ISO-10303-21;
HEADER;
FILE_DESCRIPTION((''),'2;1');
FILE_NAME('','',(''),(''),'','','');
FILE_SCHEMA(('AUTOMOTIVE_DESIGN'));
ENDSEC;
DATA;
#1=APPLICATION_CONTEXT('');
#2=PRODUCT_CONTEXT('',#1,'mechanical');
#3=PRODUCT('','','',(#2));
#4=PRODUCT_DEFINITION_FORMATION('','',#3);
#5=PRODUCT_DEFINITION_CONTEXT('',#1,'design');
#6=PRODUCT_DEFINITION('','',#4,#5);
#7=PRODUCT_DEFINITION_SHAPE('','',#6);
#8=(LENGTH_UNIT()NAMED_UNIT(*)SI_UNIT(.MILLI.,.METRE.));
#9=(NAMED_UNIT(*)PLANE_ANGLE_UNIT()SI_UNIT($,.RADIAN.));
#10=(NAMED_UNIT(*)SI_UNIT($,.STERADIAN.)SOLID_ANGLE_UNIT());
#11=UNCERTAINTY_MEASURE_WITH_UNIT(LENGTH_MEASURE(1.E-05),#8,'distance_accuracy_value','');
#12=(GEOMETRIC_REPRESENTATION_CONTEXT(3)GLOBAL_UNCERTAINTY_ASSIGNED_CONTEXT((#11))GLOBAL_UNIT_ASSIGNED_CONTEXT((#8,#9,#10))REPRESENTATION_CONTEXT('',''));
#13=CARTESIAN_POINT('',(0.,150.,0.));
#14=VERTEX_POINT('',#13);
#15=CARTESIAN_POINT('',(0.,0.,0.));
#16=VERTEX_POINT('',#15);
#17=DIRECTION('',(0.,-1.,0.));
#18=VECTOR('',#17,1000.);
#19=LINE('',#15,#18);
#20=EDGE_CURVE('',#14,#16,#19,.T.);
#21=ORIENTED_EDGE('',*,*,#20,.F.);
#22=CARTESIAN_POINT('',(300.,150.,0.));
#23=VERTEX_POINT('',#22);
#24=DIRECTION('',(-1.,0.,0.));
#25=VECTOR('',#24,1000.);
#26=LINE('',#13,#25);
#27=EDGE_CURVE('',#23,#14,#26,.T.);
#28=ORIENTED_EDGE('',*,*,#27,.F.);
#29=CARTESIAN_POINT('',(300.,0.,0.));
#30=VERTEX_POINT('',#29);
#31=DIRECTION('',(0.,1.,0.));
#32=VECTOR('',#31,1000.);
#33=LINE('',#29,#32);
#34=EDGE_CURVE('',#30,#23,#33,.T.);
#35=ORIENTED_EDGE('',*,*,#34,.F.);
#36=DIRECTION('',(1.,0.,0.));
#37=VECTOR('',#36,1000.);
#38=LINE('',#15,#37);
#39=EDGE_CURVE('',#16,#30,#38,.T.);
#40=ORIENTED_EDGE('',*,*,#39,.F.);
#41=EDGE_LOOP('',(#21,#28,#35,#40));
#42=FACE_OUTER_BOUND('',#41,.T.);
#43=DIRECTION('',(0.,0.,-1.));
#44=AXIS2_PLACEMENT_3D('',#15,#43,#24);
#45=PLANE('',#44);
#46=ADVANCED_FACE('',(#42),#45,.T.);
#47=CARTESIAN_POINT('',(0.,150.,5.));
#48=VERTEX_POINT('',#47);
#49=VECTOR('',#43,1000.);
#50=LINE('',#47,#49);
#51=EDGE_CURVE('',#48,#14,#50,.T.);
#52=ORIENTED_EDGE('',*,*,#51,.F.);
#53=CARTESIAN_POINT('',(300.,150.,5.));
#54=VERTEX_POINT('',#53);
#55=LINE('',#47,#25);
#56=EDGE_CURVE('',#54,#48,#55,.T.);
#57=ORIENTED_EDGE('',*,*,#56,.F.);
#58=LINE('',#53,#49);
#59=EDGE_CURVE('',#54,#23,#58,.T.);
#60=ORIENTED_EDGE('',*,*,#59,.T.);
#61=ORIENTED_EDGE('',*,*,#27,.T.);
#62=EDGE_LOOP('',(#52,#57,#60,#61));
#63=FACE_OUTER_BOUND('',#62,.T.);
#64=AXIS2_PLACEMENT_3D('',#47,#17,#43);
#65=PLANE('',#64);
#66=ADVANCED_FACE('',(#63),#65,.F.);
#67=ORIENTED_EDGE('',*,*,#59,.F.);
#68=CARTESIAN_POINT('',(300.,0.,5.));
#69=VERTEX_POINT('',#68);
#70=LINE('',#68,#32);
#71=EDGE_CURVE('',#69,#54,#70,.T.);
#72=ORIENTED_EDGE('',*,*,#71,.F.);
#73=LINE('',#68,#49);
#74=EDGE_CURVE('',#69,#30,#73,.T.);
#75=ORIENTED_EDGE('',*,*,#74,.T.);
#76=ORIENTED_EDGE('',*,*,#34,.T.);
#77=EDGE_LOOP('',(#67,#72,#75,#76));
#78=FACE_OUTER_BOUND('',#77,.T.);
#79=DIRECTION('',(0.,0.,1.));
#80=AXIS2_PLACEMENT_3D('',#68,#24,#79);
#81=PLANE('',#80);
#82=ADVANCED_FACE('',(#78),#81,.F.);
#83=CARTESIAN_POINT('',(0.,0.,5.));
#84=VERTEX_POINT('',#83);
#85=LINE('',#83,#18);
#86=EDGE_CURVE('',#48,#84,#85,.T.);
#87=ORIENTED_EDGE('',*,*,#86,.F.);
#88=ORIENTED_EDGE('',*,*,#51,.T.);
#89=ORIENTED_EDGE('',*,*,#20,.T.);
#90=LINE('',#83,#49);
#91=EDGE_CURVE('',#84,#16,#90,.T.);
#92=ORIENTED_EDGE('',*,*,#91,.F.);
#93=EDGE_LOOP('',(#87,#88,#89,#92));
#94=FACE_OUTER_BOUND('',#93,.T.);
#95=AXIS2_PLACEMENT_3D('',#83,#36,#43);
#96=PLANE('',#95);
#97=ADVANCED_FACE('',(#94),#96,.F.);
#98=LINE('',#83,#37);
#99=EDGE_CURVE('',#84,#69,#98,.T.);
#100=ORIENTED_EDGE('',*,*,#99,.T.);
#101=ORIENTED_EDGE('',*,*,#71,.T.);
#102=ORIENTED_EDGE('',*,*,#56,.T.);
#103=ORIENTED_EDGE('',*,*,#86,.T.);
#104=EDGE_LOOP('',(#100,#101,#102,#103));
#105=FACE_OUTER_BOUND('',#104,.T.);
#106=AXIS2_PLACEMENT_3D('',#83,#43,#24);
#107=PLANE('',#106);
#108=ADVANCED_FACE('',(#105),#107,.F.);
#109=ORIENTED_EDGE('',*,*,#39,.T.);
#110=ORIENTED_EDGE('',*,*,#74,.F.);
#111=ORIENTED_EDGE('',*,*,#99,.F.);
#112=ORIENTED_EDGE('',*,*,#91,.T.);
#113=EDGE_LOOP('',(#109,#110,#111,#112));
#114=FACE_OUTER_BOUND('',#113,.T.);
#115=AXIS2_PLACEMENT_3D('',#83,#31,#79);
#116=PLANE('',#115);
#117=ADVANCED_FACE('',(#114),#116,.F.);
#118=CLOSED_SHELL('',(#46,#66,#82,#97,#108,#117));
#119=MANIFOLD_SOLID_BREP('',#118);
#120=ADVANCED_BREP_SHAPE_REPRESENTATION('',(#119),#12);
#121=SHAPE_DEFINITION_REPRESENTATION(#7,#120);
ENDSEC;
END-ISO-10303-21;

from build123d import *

# Parameters (mm, degrees)
SKETCH1_W           = 300
SKETCH1_H           = 150
BOSS_EXTRUDE1_DEPTH = 5


with BuildPart() as part:
    # Sketch1 → Boss-Extrude1 (new body)
    with BuildSketch(Plane.XY):
        with Locations((150, 75)):
            Rectangle(SKETCH1_W, SKETCH1_H)
    extrude(amount=BOSS_EXTRUDE1_DEPTH)


solid = part.part
